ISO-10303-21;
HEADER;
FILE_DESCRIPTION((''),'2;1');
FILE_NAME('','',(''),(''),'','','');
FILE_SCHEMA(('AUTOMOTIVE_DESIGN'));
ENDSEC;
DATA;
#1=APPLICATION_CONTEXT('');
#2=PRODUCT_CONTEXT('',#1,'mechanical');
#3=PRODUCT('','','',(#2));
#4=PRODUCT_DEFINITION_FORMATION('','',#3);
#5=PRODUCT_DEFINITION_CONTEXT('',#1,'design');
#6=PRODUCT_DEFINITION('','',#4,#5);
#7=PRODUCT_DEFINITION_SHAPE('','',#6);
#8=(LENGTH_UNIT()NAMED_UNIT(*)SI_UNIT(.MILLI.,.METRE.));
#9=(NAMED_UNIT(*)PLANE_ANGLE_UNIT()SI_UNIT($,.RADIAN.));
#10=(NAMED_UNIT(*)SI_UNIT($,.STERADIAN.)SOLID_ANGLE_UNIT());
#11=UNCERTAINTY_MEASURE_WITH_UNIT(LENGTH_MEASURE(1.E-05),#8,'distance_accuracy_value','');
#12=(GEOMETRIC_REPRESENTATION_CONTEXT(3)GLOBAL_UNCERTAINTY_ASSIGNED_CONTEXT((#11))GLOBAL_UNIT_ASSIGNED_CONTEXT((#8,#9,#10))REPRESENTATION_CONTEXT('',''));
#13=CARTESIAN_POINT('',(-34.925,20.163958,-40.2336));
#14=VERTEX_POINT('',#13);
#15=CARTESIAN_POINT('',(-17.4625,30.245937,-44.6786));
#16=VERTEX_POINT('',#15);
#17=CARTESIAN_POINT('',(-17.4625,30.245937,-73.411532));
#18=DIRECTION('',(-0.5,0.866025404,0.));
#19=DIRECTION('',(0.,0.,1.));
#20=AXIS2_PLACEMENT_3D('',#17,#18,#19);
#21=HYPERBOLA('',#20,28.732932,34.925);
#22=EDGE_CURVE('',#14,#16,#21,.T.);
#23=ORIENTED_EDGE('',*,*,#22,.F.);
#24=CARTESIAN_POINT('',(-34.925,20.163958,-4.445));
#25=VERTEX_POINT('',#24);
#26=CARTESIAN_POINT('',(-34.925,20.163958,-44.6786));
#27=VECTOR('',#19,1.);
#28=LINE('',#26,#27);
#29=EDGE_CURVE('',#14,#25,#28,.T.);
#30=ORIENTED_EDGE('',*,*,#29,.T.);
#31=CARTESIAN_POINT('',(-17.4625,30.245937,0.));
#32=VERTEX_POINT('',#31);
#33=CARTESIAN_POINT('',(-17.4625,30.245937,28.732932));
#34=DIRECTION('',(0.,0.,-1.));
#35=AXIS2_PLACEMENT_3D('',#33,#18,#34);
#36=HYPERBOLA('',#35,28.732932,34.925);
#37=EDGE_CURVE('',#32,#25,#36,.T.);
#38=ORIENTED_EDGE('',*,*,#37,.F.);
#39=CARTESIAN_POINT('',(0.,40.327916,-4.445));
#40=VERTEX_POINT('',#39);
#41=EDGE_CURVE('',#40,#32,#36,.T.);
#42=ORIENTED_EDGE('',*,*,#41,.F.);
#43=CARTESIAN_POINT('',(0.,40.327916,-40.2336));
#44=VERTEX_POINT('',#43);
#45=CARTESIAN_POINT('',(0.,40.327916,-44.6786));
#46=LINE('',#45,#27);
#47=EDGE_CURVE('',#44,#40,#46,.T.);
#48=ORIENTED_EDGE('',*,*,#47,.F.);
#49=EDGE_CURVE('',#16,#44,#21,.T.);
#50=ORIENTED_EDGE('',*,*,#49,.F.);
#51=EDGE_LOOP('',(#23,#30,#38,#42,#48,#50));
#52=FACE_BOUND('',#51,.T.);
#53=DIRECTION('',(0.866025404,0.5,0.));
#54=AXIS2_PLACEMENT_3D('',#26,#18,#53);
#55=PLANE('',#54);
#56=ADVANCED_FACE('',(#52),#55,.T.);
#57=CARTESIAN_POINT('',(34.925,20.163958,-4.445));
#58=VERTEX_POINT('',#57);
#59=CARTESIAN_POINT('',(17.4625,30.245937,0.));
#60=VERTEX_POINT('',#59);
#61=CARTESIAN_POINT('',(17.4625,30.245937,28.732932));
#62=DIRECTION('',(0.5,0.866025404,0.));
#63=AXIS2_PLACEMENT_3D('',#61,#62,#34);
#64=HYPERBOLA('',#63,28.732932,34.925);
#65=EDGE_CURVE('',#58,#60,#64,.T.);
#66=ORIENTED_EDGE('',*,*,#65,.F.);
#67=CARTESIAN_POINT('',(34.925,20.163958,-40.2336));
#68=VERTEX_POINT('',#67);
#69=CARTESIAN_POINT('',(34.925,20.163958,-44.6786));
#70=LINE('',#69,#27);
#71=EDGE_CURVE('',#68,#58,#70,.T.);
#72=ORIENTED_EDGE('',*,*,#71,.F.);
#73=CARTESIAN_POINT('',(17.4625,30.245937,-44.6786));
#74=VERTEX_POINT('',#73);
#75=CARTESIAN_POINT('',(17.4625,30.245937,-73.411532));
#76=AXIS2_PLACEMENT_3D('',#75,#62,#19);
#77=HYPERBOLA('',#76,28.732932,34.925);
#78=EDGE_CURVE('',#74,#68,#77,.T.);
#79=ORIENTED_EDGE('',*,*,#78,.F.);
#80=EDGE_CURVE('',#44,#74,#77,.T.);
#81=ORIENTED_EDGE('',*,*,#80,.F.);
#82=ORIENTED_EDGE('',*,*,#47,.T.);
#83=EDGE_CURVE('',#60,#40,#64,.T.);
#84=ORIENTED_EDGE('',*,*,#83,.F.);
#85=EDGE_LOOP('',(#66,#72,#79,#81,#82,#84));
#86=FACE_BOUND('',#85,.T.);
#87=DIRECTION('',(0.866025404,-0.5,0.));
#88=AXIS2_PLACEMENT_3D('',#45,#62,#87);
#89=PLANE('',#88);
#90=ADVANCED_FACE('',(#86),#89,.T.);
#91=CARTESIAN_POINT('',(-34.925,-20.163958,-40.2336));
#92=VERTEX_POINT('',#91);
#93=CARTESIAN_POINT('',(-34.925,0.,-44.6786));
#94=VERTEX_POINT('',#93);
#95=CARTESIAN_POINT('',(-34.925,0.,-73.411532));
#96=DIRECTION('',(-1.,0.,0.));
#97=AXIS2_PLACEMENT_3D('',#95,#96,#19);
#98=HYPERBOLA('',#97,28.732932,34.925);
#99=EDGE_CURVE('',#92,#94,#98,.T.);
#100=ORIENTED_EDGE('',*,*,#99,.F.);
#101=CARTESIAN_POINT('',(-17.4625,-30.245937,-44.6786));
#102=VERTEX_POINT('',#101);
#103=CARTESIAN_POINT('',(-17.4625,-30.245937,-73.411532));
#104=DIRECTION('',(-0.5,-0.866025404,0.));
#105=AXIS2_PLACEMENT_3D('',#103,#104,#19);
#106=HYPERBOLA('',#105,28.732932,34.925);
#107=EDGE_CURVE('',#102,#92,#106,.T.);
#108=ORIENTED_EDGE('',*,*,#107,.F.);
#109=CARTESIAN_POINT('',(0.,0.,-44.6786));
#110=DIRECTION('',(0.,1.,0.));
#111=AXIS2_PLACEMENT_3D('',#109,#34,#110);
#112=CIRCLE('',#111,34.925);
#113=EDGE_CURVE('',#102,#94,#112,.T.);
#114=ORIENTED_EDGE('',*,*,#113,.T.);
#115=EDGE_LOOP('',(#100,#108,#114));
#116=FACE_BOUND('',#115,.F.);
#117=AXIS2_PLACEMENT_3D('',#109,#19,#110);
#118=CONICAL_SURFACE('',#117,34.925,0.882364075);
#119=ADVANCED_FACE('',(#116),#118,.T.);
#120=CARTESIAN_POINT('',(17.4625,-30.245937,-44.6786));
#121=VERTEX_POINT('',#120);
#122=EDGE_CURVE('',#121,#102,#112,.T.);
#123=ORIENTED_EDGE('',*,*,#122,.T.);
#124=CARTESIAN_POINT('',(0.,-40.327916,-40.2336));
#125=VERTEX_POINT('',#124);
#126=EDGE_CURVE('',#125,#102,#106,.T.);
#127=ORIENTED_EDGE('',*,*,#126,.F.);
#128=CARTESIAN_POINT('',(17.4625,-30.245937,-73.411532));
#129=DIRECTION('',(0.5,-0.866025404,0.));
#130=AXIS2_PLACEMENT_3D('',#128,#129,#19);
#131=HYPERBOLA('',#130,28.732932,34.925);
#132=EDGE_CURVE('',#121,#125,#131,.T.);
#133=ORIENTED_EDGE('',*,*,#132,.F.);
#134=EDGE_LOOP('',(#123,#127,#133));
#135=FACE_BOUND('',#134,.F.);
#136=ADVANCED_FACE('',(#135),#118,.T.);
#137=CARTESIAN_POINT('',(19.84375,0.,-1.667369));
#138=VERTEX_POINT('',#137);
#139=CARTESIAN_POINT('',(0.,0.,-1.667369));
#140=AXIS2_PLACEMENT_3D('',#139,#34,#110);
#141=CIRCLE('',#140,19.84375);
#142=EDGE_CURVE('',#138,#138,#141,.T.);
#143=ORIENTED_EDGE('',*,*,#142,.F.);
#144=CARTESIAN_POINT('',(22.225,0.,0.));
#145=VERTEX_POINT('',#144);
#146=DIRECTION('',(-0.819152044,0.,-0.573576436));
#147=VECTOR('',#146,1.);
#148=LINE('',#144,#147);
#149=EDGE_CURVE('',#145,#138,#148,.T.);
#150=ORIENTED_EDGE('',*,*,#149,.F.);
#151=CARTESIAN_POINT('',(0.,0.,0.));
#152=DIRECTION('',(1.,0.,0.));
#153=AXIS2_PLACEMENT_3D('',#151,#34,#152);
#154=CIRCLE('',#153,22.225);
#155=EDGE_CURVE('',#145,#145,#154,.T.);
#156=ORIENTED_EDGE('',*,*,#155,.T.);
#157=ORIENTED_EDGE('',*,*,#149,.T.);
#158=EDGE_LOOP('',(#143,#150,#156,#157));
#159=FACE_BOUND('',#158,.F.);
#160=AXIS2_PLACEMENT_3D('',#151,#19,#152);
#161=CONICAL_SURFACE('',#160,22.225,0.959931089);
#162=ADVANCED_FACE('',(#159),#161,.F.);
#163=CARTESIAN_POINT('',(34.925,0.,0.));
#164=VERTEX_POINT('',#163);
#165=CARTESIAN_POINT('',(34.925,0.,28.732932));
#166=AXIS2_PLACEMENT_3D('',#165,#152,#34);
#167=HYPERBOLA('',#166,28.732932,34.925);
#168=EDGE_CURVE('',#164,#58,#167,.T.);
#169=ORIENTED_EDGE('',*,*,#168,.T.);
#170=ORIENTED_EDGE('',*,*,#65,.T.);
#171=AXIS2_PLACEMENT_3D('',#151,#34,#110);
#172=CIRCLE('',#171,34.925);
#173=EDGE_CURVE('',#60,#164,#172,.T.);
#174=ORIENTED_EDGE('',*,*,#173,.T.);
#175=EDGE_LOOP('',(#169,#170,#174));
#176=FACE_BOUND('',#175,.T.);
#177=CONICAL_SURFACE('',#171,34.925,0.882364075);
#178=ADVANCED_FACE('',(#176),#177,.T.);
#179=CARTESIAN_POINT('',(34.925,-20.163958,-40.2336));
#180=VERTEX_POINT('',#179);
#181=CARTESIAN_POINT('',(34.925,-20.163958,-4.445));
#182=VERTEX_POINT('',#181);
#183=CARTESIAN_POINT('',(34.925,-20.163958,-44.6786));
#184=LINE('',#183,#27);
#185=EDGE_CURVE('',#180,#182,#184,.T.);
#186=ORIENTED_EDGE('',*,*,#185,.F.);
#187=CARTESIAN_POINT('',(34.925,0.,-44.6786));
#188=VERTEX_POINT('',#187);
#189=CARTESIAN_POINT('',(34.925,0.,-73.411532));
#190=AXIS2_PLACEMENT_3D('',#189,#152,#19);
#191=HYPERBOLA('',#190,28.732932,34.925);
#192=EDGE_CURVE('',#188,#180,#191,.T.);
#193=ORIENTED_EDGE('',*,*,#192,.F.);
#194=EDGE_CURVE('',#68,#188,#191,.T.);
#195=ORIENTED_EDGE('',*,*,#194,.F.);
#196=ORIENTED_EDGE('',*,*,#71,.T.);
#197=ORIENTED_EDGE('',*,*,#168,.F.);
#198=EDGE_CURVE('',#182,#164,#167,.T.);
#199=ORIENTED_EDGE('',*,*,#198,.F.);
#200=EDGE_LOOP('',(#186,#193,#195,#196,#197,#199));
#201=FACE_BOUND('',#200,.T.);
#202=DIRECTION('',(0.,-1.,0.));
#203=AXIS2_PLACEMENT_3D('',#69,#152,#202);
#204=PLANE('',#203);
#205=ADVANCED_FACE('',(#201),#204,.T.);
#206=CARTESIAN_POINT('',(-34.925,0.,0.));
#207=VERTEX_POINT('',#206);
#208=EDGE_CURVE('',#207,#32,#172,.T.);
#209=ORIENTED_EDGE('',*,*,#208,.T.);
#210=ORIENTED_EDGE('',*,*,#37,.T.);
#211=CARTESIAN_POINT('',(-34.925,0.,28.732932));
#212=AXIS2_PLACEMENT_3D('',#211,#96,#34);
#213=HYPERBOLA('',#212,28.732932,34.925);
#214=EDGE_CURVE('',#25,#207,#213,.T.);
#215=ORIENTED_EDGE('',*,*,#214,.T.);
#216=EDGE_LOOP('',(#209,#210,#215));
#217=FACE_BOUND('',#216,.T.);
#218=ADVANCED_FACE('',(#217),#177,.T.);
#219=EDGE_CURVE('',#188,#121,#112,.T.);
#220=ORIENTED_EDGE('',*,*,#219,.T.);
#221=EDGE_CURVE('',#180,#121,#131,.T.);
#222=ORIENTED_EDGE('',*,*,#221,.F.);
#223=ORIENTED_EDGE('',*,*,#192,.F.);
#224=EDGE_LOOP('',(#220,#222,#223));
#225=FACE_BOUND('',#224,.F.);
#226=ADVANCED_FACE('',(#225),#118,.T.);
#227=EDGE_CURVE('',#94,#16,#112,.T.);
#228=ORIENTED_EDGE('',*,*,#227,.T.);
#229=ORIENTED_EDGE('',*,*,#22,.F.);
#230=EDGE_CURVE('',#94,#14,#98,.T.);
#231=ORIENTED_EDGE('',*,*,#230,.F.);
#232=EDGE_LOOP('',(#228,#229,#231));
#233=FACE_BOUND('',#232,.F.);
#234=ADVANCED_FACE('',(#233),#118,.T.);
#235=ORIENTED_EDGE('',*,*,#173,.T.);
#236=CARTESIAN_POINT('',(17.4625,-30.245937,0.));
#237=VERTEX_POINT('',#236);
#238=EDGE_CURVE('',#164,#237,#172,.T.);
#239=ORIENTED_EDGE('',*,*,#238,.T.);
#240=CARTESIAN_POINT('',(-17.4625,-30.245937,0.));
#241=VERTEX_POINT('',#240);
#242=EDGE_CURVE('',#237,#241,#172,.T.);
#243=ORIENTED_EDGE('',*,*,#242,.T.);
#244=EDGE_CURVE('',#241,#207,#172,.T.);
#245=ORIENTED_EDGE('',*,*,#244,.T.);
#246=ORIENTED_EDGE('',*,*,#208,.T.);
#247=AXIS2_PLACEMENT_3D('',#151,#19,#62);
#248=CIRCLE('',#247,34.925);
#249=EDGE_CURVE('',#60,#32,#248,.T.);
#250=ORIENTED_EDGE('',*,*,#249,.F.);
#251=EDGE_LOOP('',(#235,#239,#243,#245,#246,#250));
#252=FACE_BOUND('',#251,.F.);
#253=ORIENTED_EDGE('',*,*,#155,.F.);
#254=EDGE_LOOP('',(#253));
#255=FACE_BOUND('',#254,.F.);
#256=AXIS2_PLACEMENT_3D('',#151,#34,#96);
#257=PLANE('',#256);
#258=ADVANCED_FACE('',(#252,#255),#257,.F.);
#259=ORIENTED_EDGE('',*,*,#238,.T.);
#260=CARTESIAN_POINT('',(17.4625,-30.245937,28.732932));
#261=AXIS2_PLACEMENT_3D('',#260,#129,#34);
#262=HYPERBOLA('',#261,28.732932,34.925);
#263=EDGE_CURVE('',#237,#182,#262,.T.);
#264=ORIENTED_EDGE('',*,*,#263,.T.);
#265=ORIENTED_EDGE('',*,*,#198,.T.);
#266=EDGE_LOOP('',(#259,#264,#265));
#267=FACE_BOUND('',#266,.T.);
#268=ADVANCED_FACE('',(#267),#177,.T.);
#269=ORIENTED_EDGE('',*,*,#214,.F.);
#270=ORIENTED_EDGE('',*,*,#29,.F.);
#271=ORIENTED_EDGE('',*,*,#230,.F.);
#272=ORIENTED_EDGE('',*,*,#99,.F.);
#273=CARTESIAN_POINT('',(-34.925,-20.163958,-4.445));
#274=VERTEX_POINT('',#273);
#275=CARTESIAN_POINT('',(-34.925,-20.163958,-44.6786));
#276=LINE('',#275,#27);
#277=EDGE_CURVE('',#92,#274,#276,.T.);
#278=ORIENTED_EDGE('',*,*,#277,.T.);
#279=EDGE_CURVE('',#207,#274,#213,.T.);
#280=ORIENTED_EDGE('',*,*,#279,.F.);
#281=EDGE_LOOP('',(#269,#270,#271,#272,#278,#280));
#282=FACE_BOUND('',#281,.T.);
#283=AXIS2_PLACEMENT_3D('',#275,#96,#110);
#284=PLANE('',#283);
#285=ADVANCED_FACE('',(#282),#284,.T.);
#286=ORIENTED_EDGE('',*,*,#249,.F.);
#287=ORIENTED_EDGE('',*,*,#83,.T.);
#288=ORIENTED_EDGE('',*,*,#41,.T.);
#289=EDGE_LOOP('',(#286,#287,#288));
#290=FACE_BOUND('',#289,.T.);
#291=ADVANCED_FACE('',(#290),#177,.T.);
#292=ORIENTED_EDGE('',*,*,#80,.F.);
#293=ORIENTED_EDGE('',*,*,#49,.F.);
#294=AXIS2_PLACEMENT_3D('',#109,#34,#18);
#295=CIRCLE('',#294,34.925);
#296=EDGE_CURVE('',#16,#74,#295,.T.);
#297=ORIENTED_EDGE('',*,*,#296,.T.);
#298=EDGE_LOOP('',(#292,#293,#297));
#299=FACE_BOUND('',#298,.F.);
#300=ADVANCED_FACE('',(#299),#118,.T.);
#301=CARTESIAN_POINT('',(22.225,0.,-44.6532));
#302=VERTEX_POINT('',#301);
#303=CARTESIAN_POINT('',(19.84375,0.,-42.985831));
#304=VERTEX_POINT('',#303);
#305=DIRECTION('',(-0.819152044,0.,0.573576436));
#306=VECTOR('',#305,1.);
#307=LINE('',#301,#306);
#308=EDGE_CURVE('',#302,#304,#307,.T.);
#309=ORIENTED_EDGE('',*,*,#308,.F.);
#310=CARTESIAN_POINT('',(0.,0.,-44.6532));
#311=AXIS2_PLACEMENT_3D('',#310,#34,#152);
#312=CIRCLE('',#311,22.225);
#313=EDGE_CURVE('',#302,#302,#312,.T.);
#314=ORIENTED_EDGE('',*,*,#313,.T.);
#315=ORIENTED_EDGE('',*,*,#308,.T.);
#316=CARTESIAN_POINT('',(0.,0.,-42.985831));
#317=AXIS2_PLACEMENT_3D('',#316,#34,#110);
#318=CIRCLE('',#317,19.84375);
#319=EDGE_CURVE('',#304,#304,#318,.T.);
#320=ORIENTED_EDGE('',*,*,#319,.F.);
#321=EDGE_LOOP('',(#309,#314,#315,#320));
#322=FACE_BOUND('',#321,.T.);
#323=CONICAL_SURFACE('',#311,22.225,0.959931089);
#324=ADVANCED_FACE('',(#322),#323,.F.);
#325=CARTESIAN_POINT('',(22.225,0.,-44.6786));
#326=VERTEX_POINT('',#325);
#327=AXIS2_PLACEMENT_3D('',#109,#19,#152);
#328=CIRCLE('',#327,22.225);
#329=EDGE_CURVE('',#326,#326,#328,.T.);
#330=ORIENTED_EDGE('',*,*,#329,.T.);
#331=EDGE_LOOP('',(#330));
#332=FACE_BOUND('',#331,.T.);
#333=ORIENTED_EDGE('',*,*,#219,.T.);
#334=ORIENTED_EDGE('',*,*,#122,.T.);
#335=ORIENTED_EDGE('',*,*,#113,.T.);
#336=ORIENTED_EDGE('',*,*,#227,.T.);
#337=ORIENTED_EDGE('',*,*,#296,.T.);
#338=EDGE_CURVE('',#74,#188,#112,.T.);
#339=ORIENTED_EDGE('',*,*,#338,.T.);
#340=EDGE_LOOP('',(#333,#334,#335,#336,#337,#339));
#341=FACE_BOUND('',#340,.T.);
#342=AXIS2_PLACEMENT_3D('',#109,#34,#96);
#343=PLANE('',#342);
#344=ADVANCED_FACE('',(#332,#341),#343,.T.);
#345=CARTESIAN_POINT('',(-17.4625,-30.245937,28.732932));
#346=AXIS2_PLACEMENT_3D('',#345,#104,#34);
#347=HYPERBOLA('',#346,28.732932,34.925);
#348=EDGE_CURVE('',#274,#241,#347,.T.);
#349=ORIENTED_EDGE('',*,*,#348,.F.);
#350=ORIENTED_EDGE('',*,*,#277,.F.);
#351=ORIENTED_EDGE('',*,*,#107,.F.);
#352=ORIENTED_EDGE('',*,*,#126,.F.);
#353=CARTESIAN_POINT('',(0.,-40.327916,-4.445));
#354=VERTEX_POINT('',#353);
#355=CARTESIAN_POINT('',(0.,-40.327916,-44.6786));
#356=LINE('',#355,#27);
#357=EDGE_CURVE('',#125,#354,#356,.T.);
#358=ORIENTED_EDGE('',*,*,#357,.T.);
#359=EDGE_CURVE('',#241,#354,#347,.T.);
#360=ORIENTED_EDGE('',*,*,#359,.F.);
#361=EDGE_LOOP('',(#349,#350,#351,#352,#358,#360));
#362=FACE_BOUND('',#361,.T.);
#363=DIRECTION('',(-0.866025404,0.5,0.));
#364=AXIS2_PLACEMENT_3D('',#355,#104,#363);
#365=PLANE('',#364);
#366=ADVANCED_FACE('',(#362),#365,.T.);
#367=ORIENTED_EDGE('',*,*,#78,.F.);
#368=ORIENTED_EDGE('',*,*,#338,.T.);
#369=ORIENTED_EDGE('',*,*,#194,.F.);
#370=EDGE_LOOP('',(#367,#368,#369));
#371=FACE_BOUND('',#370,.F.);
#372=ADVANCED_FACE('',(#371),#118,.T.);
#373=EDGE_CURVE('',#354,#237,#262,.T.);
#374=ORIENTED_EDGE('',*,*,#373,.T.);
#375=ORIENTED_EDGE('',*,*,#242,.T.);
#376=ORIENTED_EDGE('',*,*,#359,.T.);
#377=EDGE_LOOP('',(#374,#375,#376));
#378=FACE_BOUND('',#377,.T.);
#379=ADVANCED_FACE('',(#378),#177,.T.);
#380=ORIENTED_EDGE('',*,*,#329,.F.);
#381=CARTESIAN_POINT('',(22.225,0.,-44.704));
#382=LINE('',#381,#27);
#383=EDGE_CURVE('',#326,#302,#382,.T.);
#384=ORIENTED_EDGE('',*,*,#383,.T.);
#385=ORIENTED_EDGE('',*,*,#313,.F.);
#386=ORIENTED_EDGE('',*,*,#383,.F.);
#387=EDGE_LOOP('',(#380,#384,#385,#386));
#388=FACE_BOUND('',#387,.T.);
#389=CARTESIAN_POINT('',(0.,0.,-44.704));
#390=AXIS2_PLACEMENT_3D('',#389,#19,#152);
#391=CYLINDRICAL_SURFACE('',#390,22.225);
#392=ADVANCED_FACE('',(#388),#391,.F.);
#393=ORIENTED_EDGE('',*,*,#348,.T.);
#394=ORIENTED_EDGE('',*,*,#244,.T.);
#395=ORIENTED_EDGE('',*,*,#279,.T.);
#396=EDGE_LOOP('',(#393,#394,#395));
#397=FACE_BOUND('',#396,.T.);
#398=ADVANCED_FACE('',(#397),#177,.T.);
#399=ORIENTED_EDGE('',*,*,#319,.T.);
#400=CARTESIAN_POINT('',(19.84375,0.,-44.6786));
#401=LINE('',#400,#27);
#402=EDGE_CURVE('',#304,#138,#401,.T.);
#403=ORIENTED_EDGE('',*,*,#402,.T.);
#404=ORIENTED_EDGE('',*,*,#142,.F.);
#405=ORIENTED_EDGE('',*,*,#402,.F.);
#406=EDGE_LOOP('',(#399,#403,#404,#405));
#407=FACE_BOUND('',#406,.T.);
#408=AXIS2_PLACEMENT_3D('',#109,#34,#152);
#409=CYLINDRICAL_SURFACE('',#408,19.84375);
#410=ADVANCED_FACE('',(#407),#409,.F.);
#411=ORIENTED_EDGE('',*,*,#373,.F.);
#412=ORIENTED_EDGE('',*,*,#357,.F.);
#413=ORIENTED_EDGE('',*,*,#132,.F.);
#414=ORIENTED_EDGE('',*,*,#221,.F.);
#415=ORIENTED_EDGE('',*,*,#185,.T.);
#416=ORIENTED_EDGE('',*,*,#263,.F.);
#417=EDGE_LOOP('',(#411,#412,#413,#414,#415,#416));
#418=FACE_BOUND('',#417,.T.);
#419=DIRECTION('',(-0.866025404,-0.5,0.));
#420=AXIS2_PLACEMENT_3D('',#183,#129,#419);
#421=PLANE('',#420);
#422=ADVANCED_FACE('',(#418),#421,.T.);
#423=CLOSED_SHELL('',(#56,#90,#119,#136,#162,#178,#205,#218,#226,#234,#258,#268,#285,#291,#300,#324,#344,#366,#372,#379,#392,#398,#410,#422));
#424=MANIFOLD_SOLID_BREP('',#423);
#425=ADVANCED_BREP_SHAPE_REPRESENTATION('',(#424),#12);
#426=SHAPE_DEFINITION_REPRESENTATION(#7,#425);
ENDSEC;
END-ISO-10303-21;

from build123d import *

# Parameters (mm, degrees)
BASENUT_START = -44.6786
BASENUTSKE_R  = 19.84375
BASENUT_DEPTH = 44.6786


with BuildPart() as part:
    # BaseNutSke → BaseNut (new body)
    with BuildSketch(Plane.XY.offset(BASENUT_START)):
        Polygon((34.925, 20.163958151), (34.925, -20.163958151), (0, -40.327916303), (-34.925, -20.163958151), (-34.925, 20.163958151), (0, 40.327916303), align=None)
        Circle(BASENUTSKE_R, mode=Mode.SUBTRACT)
    extrude(amount=BASENUT_DEPTH)

    # Sketch3 → Double-Chamfer (revolve, cut)
    with BuildSketch(Plane(origin=(0, 0, 0), x_dir=(0, 0, -1), z_dir=(1, 0, 0))):
        Polygon((44.6786, 34.925), (40.2336, 40.327916303), (40.2336, 53.027916303), (57.3786, 53.027916303), (57.3786, 34.925), align=None)
        Polygon((4.445, 53.027916303), (-12.7, 53.027916303), (-12.7, 34.925), (0, 34.925), (4.445, 40.327916303), align=None)
    revolve(axis=Axis((0, 0, 0), (0, 0, -1)), mode=Mode.SUBTRACT)

    # Sketch5 → EndChamfer (revolve, cut)
    with BuildSketch(Plane(origin=(0, 0, 0), x_dir=(0, 0, -1), z_dir=(1, 0, 0)), mode=Mode.PRIVATE) as endchamfer_sk:
        Polygon((44.6532, 22.225), (42.81909388, 19.605625), (44.704, 19.605625), (44.704, 22.225), align=None)
        Polygon((-0.0508, 22.225), (0, 22.225), (1.83410612, 19.605625), (-0.0508, 19.605625), align=None)
    revolve(endchamfer_sk.sketch.rotate(Axis((0, 0, -25.037505729), (0, 0, -1)), 90), axis=Axis((0, 0, -25.037505729), (0, 0, -1)), mode=Mode.SUBTRACT)


solid = part.part
